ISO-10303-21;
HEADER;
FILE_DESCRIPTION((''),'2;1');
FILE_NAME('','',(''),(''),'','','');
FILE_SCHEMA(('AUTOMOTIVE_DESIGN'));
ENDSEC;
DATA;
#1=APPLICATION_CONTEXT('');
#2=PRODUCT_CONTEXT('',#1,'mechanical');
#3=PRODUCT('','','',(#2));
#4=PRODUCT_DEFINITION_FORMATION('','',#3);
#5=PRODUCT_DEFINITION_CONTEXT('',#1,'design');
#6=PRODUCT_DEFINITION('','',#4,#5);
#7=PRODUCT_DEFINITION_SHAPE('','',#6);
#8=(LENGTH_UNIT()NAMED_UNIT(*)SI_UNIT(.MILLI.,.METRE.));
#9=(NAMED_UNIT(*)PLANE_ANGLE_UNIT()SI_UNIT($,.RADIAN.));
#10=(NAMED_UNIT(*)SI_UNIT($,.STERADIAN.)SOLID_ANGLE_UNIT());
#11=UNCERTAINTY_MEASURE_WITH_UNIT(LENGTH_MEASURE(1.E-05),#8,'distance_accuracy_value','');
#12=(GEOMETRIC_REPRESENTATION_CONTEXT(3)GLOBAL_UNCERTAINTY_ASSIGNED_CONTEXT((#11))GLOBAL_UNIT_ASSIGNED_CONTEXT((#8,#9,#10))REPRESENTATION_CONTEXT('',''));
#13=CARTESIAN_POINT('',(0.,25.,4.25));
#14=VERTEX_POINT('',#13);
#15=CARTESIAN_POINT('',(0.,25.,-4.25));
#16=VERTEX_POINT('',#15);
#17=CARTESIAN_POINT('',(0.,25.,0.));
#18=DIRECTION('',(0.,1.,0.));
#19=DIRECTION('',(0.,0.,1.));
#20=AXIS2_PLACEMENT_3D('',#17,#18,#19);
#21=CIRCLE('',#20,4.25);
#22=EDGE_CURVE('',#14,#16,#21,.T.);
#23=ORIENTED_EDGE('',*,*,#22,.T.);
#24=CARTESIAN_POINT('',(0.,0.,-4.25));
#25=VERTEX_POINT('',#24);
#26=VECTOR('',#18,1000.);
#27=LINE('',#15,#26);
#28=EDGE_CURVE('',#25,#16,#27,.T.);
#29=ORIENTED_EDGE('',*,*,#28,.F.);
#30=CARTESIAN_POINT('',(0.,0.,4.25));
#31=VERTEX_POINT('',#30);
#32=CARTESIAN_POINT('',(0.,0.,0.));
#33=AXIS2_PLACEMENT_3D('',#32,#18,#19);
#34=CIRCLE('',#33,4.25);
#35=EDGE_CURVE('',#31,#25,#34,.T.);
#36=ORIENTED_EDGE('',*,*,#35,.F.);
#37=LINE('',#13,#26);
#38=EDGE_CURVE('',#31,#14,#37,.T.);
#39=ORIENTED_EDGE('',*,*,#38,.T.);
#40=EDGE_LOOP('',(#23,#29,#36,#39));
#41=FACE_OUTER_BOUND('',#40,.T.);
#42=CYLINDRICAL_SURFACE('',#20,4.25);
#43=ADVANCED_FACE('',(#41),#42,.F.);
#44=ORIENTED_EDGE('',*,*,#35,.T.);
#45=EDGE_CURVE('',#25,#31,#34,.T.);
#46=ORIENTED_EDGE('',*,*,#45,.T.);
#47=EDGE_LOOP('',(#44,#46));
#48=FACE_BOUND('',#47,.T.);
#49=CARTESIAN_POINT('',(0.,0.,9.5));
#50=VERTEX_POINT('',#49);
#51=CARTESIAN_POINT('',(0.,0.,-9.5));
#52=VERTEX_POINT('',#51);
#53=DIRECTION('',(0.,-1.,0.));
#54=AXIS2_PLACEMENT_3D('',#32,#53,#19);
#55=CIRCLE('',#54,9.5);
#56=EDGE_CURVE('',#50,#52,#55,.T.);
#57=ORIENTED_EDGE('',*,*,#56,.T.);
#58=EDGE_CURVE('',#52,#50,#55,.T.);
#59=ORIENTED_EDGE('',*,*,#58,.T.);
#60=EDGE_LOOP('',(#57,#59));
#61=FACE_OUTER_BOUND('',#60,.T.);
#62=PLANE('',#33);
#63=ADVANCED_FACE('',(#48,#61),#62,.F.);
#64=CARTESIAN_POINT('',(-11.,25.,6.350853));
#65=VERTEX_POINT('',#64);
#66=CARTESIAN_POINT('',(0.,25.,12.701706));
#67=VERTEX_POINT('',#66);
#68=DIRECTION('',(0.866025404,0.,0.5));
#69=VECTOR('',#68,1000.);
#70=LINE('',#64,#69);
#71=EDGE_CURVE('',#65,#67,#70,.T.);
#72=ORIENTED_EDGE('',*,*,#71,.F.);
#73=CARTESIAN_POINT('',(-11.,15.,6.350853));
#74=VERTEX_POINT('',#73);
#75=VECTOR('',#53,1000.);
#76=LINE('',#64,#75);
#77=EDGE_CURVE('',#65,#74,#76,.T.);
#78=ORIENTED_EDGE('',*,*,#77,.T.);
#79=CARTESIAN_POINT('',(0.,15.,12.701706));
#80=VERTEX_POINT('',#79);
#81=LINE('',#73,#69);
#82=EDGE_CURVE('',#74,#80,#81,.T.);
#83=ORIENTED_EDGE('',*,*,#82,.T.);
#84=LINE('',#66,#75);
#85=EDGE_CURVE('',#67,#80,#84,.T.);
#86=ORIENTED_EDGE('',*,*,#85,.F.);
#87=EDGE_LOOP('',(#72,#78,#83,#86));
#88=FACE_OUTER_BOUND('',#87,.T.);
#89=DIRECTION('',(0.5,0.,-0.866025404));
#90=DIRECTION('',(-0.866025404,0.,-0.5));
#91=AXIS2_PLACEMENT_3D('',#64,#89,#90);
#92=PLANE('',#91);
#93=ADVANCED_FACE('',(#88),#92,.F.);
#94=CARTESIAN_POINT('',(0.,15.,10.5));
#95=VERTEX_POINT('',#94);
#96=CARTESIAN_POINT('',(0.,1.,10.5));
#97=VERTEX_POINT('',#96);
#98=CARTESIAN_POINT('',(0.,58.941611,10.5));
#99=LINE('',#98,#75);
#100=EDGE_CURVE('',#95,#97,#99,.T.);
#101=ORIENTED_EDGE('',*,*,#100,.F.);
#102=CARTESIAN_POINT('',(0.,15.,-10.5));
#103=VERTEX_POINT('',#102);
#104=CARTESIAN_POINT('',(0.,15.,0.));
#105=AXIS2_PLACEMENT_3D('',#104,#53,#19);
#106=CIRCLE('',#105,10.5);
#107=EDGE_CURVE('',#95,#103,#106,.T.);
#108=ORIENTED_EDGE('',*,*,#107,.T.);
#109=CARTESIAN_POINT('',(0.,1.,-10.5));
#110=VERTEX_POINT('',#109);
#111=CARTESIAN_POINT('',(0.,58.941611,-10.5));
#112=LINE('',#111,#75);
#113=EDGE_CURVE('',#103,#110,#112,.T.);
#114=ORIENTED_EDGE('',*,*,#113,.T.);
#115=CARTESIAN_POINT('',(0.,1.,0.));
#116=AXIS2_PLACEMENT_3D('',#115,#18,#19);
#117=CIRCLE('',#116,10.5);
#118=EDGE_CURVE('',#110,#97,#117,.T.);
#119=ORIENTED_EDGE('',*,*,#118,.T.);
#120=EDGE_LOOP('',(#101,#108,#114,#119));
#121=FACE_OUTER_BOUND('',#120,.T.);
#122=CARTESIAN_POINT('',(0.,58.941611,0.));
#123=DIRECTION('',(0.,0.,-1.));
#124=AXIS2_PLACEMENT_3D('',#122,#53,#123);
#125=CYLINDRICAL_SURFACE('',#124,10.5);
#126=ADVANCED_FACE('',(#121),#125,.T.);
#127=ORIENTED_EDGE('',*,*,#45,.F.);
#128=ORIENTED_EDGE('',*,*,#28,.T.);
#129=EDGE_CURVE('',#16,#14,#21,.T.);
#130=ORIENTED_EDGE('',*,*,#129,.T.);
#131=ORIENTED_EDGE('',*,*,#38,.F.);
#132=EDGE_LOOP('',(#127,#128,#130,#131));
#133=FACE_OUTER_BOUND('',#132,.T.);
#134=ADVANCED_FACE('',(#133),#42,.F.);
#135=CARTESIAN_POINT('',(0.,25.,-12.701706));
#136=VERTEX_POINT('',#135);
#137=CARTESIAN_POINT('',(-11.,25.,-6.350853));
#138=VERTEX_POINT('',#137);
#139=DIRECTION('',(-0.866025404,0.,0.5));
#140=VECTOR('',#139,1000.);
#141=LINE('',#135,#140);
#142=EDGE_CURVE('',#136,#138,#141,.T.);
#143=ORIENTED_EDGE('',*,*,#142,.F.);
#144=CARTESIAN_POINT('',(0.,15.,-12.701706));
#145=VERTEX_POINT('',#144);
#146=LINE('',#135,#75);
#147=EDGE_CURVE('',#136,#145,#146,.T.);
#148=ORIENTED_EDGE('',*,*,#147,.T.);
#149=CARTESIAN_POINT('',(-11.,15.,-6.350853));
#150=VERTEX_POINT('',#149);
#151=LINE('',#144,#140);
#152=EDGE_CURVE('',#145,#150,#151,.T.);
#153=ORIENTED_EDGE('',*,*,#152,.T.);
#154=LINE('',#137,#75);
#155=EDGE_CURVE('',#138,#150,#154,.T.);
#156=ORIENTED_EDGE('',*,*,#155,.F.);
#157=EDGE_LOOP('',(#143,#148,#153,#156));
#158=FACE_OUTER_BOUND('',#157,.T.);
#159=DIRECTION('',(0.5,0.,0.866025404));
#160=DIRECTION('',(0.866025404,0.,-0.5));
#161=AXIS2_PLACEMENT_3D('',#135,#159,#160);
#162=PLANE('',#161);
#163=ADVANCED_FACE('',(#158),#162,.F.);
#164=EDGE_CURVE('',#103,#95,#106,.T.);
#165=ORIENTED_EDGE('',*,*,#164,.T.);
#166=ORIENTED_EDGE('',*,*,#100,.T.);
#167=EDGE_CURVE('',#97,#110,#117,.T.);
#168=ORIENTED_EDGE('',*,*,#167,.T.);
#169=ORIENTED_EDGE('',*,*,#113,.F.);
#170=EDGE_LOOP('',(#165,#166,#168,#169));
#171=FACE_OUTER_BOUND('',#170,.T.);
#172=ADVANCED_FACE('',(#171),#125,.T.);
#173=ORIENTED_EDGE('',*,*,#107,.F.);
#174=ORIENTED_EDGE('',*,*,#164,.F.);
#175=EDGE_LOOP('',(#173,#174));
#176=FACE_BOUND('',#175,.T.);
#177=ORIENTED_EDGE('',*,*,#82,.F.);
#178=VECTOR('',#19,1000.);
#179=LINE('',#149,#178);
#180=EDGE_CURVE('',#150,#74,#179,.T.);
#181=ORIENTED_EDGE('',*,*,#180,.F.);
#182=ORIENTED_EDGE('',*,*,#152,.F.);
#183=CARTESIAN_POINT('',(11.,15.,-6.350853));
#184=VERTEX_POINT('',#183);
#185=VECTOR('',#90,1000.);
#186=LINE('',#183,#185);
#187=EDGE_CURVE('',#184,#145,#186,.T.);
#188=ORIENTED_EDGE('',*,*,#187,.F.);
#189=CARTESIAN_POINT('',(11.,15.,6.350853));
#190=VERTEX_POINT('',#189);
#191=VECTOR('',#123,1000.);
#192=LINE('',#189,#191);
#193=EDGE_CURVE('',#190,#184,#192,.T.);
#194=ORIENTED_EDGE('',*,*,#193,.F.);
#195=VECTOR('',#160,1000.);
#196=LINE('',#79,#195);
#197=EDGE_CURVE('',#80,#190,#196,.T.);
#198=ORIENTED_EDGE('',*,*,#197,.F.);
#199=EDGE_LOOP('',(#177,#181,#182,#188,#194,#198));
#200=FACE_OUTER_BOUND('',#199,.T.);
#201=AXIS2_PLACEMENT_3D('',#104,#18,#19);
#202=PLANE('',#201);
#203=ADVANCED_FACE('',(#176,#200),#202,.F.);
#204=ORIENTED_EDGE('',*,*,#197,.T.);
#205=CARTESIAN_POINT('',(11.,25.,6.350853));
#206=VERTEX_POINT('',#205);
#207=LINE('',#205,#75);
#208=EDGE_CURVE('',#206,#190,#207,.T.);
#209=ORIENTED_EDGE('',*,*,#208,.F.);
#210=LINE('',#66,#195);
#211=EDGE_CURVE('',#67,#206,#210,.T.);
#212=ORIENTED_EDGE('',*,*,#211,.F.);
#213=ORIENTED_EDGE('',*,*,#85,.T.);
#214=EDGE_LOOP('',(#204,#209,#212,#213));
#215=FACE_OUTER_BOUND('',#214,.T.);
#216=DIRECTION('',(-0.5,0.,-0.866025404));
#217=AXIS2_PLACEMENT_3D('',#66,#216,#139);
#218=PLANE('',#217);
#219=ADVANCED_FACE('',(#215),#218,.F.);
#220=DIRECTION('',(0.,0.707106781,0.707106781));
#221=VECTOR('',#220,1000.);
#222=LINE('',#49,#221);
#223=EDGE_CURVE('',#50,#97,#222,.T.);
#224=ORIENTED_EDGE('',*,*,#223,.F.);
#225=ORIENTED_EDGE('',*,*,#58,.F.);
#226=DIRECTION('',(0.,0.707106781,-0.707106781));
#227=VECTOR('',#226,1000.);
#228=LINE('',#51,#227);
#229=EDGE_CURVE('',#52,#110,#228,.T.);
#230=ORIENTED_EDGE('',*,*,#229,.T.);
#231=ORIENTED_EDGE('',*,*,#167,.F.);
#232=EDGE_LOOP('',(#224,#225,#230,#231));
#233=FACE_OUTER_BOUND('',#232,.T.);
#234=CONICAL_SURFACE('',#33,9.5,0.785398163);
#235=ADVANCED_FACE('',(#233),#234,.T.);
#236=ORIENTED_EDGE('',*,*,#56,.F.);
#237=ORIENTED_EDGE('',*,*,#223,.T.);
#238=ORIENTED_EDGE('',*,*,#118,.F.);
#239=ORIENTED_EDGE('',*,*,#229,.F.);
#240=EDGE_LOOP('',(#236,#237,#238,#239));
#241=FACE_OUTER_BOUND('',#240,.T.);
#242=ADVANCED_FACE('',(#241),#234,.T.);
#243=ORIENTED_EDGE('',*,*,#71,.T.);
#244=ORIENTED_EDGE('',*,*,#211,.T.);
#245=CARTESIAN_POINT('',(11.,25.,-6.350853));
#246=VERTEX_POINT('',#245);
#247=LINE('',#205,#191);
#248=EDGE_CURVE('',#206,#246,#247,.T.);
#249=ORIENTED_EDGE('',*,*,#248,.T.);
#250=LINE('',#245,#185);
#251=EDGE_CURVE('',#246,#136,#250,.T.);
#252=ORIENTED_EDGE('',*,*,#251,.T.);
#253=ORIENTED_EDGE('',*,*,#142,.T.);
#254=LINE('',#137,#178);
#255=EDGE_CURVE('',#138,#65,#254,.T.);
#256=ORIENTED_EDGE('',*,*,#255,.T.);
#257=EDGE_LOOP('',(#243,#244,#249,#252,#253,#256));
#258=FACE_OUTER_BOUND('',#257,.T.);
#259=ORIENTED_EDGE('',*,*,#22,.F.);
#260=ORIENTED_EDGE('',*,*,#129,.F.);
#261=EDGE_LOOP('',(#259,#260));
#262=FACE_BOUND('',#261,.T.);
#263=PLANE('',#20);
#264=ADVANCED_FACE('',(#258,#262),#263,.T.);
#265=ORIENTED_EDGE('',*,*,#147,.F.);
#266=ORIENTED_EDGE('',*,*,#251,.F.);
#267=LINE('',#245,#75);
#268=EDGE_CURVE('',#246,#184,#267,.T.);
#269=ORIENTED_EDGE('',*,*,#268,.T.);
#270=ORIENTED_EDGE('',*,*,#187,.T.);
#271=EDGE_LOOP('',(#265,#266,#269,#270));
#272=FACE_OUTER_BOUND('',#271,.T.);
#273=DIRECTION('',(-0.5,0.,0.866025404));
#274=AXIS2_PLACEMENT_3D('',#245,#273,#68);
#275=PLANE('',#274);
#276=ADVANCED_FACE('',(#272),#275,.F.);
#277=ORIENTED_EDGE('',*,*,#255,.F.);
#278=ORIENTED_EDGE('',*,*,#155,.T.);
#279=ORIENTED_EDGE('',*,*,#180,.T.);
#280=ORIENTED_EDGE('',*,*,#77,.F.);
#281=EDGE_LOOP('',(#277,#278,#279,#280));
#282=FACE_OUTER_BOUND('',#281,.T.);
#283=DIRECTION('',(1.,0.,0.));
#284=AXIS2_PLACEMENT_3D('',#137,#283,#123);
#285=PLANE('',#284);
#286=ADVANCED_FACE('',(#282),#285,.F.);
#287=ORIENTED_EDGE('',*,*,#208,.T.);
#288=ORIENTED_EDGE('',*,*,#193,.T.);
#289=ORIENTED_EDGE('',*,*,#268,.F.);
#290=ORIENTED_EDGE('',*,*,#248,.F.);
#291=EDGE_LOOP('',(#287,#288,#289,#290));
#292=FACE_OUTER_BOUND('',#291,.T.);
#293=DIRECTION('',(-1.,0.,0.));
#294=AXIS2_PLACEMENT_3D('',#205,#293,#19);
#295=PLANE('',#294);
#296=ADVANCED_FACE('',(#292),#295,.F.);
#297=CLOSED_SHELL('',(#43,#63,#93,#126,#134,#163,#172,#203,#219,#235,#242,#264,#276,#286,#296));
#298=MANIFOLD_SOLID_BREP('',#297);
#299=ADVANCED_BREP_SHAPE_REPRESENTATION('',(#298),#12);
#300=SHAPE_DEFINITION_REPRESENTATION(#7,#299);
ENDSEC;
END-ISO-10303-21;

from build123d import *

# Parameters (mm, degrees)
BOSS_EXTRUDE1_DEPTH = 25
SKETCH3_OUTSIDE_W   = 32.376
SKETCH3_OUTSIDE_H   = 35.78
SKETCH3_OUTSIDE_R   = 10.5
CUT_EXTRUDE1_DEPTH  = 15
CHAMFER1_SIZE       = 1
M10_TAPPED_HOLE1_D  = 8.5


with BuildPart() as part:
    # Sketch1 → Boss-Extrude1 (new body)
    with BuildSketch(Plane(origin=(0, 0, 0), x_dir=(1, 0, 0), z_dir=(0, 1, 0))):
        Polygon((11, -6.350852961), (11, 6.350852961), (0, 12.701705922), (-11, 6.350852961), (-11, -6.350852961), (0, -12.701705922), align=None)
    extrude(amount=BOSS_EXTRUDE1_DEPTH)

    # Sketch3 outside → Cut-Extrude1 (cut)
    with BuildSketch(Plane.XZ):
        Rectangle(SKETCH3_OUTSIDE_W, SKETCH3_OUTSIDE_H)
        with Locations(Location((0, 0, 0), (0, 0, 270))):
            Circle(SKETCH3_OUTSIDE_R, mode=Mode.SUBTRACT)
    extrude(amount=-CUT_EXTRUDE1_DEPTH, mode=Mode.SUBTRACT)

    # Chamfer1
    chamfer1_edges = [part.edges().sort_by_distance(p)[0] for p in [
        (0, 0, 10.5),
    ]]
    chamfer(chamfer1_edges, length=CHAMFER1_SIZE)

    # M10 Tapped Hole1 (through all)
    with Locations(Plane.ZX.offset(25)):
        with Locations((0, 0)):
            Hole(M10_TAPPED_HOLE1_D / 2)


solid = part.part
